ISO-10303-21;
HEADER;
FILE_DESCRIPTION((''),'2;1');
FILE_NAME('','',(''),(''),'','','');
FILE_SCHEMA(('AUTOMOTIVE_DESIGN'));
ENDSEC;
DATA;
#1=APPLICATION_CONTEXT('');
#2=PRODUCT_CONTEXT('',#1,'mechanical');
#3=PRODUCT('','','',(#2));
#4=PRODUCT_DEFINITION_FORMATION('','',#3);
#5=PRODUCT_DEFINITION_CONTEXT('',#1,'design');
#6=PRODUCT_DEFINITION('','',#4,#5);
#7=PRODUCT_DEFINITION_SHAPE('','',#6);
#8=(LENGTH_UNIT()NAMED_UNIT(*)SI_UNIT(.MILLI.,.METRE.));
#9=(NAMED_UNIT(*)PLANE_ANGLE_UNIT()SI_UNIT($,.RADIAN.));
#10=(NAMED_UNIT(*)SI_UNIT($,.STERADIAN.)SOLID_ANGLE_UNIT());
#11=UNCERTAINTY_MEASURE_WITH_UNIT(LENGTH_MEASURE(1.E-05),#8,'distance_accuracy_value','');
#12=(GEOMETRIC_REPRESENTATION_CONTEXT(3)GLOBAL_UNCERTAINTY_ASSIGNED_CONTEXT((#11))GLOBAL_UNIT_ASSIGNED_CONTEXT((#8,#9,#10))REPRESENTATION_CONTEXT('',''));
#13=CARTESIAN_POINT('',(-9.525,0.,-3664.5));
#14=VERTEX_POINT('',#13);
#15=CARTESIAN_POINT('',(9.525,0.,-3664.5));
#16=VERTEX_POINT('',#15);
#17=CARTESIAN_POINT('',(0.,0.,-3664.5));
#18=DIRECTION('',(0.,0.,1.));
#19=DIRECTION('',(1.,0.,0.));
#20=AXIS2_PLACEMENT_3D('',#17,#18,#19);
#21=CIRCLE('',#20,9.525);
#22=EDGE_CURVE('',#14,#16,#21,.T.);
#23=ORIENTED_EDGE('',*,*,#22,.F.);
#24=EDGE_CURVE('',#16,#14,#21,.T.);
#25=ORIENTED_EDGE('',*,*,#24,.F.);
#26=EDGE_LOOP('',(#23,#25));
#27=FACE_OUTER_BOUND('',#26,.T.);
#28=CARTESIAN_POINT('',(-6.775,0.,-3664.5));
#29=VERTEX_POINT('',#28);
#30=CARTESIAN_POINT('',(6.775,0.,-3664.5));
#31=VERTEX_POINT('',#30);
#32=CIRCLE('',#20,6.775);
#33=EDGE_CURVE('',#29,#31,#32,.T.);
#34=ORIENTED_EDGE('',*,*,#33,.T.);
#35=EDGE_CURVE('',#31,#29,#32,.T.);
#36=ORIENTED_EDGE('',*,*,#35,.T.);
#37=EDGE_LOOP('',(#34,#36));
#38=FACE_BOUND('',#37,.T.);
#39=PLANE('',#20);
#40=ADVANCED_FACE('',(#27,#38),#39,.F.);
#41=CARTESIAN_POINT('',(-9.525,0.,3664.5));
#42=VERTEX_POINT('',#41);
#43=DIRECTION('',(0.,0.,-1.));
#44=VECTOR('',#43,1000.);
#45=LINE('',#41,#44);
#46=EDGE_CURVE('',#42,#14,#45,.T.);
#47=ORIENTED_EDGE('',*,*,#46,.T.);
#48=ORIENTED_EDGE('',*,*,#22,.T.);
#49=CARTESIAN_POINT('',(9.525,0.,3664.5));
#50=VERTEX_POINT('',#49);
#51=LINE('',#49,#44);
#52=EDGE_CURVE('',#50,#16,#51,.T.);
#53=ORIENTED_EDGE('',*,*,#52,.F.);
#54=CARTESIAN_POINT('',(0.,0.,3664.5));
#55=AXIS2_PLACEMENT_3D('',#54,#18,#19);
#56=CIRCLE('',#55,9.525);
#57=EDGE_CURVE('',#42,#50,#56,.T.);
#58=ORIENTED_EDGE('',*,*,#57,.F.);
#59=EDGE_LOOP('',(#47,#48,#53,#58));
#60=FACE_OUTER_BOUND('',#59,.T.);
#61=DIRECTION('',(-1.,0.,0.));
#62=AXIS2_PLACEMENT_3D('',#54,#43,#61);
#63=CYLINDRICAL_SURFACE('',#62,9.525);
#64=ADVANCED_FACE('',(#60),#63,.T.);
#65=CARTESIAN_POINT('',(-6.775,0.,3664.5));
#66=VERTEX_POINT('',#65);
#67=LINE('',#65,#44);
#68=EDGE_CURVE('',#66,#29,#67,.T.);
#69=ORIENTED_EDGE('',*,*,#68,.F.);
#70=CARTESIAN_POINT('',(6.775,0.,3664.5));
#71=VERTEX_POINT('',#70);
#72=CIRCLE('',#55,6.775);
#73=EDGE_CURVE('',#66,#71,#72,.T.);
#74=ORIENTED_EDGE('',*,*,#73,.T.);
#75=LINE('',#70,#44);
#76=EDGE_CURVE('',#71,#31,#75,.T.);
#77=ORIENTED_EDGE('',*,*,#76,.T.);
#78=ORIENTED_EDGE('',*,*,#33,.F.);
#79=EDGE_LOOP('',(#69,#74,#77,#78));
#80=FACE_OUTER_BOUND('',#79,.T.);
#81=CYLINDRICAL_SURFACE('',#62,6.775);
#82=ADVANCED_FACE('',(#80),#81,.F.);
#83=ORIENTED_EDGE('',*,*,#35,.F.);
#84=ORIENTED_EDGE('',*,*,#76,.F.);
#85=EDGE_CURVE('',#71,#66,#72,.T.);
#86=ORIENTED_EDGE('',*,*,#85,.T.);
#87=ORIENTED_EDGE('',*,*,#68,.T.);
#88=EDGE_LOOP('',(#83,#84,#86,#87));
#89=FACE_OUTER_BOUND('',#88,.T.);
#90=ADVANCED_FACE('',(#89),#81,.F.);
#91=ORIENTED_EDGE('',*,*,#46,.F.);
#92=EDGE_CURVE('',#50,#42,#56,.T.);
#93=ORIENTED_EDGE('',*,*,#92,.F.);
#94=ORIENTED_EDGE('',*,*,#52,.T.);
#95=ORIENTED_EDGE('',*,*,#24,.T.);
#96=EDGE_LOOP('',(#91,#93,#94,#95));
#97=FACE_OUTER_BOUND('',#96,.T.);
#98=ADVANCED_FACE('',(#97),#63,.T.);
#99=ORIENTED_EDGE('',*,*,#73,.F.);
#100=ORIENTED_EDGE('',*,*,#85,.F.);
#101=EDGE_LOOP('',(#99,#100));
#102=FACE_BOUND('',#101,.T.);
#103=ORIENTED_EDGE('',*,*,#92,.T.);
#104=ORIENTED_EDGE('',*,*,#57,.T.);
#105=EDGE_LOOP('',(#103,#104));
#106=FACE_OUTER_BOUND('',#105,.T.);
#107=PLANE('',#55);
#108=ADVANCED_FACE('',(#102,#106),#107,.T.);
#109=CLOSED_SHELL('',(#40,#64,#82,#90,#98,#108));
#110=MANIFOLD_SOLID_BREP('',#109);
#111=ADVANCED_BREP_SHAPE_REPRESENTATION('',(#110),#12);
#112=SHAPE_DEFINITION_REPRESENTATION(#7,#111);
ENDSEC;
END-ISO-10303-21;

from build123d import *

# Parameters (mm, degrees)
SKETCH1_R           = 9.525
SKETCH1_R_2         = 6.775
BOSS_EXTRUDE1_DEPTH = 3664.5


with BuildPart() as part:
    # Sketch1 → Boss-Extrude1 (new, symmetric)
    with BuildSketch(Plane.XY):
        Circle(SKETCH1_R)
        Circle(SKETCH1_R_2, mode=Mode.SUBTRACT)
    extrude(amount=BOSS_EXTRUDE1_DEPTH, both=True)


solid = part.part
